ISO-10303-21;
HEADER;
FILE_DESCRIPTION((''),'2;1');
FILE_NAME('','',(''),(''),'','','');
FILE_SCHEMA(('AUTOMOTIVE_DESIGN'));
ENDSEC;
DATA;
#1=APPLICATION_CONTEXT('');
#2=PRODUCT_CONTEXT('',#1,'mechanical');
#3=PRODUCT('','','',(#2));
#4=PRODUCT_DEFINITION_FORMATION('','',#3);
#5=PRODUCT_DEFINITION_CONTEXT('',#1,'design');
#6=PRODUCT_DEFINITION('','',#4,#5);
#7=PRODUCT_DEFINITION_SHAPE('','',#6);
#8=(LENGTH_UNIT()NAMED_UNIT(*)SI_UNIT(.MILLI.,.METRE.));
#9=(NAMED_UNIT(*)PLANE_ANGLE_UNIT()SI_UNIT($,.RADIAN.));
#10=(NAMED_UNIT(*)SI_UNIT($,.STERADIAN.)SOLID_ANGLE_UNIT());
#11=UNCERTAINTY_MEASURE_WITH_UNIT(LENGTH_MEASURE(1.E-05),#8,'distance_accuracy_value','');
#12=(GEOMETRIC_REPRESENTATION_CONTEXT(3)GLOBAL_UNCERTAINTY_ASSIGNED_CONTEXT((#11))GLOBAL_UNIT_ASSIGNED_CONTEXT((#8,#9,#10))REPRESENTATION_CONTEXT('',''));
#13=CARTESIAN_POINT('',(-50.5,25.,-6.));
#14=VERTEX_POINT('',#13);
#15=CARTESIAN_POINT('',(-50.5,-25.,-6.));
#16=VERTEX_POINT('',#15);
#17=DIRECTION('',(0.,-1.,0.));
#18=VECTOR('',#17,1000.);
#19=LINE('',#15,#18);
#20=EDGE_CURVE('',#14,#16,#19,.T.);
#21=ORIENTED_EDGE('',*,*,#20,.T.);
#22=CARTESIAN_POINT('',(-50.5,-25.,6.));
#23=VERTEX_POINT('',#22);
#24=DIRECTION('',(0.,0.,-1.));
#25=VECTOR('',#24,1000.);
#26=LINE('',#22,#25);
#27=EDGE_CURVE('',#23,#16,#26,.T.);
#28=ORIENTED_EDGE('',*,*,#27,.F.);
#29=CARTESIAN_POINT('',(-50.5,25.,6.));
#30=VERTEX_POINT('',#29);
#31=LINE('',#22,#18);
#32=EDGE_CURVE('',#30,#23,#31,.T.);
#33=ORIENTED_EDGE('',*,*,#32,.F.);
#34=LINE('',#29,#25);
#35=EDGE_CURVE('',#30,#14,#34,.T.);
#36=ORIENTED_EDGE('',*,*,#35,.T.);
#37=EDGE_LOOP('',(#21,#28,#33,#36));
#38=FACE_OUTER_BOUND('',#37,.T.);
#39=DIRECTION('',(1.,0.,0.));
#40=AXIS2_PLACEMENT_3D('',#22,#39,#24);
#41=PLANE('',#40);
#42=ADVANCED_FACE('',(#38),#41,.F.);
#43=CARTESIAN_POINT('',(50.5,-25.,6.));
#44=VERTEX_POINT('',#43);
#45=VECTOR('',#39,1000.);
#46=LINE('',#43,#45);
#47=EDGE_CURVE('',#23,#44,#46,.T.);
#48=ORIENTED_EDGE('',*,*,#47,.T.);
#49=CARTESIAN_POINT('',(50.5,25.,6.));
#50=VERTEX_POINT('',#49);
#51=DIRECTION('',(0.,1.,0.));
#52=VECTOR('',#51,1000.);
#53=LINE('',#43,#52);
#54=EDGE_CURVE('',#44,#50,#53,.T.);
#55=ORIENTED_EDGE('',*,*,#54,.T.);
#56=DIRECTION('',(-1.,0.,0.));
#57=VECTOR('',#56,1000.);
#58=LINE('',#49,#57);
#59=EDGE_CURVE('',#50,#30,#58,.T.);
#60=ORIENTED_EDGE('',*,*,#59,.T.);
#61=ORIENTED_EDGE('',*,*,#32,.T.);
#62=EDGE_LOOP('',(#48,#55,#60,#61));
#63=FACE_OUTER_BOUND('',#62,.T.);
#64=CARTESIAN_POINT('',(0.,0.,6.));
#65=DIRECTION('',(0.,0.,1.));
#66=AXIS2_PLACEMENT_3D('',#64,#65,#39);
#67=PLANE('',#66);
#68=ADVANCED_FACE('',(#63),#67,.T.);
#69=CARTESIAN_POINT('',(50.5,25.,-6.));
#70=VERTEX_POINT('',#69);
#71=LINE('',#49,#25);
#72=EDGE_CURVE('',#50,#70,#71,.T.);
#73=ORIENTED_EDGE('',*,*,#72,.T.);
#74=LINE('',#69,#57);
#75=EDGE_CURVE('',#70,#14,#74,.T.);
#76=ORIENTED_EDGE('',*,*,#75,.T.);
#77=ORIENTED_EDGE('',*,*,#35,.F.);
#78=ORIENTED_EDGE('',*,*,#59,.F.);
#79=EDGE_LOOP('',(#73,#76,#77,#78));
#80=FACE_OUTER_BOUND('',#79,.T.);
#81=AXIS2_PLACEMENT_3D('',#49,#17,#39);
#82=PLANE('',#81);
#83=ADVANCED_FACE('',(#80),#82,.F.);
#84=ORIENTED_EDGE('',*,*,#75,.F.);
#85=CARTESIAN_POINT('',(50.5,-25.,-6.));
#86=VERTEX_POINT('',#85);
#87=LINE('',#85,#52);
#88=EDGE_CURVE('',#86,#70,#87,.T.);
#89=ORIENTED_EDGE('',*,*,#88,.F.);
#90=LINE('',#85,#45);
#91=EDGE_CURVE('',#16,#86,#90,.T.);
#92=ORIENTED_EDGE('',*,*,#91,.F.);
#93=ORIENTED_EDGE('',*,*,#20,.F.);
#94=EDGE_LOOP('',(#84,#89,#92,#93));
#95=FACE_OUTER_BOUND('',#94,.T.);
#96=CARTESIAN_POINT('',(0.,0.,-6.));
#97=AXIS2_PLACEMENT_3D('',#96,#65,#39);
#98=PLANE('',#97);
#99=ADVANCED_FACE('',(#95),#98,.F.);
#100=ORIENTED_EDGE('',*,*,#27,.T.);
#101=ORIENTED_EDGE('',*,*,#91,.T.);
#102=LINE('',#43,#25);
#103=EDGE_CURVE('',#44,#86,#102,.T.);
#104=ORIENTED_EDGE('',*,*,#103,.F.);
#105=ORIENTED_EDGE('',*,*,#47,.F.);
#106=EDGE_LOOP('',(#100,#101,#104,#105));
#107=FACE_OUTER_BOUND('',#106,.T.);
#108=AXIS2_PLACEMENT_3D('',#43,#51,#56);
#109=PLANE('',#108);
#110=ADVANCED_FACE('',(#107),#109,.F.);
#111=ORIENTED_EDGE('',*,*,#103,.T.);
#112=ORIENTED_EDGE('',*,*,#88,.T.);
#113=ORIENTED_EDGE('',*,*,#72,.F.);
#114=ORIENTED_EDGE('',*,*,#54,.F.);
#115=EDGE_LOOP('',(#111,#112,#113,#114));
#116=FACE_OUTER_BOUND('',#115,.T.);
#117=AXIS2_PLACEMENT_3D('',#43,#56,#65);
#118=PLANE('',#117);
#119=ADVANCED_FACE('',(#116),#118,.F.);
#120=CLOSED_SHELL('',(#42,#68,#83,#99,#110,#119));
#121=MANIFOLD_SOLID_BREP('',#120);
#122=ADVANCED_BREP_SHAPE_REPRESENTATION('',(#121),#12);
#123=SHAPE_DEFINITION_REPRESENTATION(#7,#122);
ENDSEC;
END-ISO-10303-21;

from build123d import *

# Parameters (mm, degrees)
SKETCH1_W           = 101
SKETCH1_H           = 50
BOSS_EXTRUDE1_DEPTH = 6


with BuildPart() as part:
    # Sketch1 → Boss-Extrude1 (new, symmetric)
    with BuildSketch(Plane.XY):
        Rectangle(SKETCH1_W, SKETCH1_H)
    extrude(amount=BOSS_EXTRUDE1_DEPTH, both=True)


solid = part.part
